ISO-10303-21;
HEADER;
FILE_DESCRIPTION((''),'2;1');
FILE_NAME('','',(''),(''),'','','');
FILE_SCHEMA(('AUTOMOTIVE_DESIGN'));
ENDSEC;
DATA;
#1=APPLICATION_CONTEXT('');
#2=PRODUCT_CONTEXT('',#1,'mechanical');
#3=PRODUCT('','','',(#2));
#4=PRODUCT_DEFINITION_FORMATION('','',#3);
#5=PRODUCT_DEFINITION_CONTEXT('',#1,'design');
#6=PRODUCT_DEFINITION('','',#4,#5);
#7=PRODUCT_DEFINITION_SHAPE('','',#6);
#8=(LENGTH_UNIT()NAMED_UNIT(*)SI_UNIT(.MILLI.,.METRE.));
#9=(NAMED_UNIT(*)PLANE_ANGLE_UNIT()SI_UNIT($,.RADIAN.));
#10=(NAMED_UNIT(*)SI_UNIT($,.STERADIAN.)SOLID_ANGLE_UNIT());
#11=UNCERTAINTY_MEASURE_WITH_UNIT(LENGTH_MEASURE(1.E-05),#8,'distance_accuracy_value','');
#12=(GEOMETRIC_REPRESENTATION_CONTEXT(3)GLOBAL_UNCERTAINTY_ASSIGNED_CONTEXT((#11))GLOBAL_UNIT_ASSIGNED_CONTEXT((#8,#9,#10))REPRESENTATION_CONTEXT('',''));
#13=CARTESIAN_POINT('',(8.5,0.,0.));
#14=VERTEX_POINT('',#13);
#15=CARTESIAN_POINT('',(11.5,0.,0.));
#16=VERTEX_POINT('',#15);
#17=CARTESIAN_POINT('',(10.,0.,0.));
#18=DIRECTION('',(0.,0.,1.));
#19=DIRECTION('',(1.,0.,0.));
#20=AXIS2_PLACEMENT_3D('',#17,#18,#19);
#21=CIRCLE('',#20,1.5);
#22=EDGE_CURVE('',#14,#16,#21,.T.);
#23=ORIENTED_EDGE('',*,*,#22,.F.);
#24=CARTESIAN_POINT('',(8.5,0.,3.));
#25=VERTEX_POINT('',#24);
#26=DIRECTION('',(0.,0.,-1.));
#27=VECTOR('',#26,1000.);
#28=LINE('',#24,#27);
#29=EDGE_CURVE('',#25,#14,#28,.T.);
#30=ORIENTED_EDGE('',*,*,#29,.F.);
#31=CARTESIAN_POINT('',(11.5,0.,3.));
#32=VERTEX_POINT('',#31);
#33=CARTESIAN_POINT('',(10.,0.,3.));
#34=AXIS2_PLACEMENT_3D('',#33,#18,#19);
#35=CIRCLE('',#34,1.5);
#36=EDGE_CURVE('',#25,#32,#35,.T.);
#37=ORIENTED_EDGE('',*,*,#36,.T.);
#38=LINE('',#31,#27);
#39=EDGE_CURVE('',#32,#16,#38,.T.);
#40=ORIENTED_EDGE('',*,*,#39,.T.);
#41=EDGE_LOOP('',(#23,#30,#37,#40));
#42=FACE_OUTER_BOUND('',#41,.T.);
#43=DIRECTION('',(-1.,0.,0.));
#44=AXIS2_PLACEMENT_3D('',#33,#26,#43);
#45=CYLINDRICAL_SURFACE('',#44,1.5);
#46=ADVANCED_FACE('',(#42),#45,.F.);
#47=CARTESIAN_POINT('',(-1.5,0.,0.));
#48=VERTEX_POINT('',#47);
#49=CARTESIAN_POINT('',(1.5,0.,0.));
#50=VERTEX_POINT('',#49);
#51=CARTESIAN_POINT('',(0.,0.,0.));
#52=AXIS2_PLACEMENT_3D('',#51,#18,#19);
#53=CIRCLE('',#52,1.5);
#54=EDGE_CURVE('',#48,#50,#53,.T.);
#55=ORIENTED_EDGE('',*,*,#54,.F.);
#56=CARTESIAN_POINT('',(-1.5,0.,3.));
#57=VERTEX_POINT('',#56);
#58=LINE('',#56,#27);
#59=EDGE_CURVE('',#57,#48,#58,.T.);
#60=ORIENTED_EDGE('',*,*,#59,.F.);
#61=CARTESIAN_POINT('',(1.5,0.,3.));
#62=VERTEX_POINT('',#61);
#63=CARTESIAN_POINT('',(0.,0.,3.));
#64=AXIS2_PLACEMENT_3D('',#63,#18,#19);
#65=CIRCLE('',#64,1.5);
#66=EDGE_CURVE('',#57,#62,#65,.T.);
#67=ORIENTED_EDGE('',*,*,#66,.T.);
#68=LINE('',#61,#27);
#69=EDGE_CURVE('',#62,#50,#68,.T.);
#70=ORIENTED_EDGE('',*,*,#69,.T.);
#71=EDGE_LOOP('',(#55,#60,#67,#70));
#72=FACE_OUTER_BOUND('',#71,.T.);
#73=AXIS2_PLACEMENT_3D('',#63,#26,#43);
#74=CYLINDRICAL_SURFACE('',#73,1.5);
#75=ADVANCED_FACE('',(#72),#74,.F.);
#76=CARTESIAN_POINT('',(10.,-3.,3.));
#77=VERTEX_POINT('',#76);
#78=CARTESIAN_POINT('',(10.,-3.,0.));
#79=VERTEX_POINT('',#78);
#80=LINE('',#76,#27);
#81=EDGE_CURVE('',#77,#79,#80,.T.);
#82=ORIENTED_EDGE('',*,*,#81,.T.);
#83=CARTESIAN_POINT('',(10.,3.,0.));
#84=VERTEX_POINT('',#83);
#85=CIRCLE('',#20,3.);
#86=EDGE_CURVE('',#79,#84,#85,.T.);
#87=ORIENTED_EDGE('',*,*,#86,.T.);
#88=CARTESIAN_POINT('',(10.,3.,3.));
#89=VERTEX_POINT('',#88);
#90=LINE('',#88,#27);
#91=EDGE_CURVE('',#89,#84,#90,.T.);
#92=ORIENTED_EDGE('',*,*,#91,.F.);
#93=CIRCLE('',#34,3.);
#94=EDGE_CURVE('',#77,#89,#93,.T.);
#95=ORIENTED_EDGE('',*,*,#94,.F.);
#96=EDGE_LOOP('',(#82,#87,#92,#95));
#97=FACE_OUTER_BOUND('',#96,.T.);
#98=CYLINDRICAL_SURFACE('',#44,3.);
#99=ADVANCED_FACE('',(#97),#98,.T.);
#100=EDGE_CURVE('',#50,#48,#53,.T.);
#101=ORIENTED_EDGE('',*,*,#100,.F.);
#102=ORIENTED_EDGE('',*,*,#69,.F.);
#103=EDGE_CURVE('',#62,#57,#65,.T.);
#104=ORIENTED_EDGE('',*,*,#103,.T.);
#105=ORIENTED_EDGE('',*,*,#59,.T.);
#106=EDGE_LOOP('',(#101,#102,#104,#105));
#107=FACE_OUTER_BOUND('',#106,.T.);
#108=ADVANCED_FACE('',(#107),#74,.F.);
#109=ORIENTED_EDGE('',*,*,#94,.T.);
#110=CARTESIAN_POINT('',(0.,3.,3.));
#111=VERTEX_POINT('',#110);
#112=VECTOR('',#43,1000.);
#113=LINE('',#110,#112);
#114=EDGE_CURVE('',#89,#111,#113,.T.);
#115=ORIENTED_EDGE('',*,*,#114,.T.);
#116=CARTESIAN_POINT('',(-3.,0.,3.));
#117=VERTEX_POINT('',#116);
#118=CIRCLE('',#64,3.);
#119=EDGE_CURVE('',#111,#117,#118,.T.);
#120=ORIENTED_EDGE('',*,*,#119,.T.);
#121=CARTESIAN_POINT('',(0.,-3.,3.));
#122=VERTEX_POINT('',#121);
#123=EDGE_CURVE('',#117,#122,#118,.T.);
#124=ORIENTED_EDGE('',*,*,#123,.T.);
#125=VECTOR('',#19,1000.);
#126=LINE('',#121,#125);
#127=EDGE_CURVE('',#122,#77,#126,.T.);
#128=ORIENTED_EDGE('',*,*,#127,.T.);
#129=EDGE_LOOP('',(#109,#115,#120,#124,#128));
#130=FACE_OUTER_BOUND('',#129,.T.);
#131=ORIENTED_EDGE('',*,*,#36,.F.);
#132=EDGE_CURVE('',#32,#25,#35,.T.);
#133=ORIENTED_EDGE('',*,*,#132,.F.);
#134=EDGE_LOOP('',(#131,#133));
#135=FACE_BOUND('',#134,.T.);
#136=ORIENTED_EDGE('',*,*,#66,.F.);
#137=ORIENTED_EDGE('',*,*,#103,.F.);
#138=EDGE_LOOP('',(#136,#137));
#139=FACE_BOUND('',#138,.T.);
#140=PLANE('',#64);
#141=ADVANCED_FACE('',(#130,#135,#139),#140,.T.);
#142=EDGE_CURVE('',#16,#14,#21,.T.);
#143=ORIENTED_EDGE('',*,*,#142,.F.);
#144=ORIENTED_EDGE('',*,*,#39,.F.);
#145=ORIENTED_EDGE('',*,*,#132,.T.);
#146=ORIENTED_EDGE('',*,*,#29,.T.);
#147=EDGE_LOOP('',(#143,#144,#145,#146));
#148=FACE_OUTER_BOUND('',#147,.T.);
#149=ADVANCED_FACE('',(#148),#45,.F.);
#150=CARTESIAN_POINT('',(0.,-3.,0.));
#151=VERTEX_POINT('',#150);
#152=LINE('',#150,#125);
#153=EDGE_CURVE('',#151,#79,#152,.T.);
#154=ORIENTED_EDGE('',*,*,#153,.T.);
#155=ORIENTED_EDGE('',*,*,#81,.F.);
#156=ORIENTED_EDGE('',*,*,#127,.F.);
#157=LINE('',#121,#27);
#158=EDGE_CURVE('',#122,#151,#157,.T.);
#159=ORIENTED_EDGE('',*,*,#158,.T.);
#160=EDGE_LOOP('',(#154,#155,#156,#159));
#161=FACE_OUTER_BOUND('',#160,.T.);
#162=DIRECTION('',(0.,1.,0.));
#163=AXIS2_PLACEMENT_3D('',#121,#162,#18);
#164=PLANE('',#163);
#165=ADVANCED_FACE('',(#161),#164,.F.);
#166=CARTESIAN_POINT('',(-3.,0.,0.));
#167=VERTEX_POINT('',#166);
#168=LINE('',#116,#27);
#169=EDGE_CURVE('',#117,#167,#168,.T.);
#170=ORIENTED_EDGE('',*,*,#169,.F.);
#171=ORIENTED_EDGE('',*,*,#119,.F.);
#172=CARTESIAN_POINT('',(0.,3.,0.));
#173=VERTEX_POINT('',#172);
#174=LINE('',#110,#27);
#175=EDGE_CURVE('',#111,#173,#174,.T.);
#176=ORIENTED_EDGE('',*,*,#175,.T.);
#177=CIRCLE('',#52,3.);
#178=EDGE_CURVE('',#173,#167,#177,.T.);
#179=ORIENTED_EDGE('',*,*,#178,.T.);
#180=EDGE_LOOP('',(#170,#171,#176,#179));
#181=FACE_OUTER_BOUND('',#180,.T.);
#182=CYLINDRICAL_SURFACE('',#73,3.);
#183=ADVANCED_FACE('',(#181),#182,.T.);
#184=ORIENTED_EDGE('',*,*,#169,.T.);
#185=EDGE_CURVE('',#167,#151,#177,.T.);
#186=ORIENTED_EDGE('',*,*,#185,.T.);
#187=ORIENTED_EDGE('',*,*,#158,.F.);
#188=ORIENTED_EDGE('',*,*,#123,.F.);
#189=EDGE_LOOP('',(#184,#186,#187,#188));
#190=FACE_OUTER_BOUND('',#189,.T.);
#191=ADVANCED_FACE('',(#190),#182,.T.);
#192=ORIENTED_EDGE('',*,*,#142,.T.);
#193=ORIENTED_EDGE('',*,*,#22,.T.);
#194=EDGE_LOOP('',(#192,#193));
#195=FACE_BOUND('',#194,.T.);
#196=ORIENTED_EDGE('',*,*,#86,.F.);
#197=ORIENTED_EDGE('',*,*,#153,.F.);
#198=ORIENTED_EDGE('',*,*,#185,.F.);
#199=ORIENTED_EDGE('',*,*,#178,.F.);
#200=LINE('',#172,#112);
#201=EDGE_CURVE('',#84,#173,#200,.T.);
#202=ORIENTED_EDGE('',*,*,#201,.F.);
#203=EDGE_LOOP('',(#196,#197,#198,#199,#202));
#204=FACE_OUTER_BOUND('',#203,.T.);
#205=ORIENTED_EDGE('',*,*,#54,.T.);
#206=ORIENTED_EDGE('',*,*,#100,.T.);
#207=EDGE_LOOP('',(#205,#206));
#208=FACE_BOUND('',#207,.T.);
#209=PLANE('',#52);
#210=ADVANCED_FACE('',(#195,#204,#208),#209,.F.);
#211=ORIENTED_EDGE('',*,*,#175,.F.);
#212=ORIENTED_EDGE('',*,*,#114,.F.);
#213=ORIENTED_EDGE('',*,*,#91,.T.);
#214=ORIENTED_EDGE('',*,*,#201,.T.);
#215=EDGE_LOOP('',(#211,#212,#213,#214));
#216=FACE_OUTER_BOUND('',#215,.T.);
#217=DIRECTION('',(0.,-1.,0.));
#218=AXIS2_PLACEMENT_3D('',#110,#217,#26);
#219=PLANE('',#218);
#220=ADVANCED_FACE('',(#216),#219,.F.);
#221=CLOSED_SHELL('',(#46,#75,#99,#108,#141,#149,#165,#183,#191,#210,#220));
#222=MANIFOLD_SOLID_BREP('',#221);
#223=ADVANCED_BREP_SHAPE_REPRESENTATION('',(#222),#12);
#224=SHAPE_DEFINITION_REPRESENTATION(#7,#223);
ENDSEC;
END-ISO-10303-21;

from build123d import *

# Parameters (mm, degrees)
SKETCH1_R           = 1.5
BOSS_EXTRUDE1_DEPTH = 3


with BuildPart() as part:
    # Sketch1 → Boss-Extrude1 (new body)
    with BuildSketch(Plane.XY):
        with BuildLine():
            Line((0, 3), (10, 3))
            ThreePointArc((10, 3), (13, 0), (10, -3))
            Line((10, -3), (0, -3))
            ThreePointArc((0, -3), (-3, 0), (0, 3))
        make_face()
        Circle(SKETCH1_R, mode=Mode.SUBTRACT)
        with Locations((10, 0)):
            Circle(SKETCH1_R, mode=Mode.SUBTRACT)
    extrude(amount=BOSS_EXTRUDE1_DEPTH)


solid = part.part
